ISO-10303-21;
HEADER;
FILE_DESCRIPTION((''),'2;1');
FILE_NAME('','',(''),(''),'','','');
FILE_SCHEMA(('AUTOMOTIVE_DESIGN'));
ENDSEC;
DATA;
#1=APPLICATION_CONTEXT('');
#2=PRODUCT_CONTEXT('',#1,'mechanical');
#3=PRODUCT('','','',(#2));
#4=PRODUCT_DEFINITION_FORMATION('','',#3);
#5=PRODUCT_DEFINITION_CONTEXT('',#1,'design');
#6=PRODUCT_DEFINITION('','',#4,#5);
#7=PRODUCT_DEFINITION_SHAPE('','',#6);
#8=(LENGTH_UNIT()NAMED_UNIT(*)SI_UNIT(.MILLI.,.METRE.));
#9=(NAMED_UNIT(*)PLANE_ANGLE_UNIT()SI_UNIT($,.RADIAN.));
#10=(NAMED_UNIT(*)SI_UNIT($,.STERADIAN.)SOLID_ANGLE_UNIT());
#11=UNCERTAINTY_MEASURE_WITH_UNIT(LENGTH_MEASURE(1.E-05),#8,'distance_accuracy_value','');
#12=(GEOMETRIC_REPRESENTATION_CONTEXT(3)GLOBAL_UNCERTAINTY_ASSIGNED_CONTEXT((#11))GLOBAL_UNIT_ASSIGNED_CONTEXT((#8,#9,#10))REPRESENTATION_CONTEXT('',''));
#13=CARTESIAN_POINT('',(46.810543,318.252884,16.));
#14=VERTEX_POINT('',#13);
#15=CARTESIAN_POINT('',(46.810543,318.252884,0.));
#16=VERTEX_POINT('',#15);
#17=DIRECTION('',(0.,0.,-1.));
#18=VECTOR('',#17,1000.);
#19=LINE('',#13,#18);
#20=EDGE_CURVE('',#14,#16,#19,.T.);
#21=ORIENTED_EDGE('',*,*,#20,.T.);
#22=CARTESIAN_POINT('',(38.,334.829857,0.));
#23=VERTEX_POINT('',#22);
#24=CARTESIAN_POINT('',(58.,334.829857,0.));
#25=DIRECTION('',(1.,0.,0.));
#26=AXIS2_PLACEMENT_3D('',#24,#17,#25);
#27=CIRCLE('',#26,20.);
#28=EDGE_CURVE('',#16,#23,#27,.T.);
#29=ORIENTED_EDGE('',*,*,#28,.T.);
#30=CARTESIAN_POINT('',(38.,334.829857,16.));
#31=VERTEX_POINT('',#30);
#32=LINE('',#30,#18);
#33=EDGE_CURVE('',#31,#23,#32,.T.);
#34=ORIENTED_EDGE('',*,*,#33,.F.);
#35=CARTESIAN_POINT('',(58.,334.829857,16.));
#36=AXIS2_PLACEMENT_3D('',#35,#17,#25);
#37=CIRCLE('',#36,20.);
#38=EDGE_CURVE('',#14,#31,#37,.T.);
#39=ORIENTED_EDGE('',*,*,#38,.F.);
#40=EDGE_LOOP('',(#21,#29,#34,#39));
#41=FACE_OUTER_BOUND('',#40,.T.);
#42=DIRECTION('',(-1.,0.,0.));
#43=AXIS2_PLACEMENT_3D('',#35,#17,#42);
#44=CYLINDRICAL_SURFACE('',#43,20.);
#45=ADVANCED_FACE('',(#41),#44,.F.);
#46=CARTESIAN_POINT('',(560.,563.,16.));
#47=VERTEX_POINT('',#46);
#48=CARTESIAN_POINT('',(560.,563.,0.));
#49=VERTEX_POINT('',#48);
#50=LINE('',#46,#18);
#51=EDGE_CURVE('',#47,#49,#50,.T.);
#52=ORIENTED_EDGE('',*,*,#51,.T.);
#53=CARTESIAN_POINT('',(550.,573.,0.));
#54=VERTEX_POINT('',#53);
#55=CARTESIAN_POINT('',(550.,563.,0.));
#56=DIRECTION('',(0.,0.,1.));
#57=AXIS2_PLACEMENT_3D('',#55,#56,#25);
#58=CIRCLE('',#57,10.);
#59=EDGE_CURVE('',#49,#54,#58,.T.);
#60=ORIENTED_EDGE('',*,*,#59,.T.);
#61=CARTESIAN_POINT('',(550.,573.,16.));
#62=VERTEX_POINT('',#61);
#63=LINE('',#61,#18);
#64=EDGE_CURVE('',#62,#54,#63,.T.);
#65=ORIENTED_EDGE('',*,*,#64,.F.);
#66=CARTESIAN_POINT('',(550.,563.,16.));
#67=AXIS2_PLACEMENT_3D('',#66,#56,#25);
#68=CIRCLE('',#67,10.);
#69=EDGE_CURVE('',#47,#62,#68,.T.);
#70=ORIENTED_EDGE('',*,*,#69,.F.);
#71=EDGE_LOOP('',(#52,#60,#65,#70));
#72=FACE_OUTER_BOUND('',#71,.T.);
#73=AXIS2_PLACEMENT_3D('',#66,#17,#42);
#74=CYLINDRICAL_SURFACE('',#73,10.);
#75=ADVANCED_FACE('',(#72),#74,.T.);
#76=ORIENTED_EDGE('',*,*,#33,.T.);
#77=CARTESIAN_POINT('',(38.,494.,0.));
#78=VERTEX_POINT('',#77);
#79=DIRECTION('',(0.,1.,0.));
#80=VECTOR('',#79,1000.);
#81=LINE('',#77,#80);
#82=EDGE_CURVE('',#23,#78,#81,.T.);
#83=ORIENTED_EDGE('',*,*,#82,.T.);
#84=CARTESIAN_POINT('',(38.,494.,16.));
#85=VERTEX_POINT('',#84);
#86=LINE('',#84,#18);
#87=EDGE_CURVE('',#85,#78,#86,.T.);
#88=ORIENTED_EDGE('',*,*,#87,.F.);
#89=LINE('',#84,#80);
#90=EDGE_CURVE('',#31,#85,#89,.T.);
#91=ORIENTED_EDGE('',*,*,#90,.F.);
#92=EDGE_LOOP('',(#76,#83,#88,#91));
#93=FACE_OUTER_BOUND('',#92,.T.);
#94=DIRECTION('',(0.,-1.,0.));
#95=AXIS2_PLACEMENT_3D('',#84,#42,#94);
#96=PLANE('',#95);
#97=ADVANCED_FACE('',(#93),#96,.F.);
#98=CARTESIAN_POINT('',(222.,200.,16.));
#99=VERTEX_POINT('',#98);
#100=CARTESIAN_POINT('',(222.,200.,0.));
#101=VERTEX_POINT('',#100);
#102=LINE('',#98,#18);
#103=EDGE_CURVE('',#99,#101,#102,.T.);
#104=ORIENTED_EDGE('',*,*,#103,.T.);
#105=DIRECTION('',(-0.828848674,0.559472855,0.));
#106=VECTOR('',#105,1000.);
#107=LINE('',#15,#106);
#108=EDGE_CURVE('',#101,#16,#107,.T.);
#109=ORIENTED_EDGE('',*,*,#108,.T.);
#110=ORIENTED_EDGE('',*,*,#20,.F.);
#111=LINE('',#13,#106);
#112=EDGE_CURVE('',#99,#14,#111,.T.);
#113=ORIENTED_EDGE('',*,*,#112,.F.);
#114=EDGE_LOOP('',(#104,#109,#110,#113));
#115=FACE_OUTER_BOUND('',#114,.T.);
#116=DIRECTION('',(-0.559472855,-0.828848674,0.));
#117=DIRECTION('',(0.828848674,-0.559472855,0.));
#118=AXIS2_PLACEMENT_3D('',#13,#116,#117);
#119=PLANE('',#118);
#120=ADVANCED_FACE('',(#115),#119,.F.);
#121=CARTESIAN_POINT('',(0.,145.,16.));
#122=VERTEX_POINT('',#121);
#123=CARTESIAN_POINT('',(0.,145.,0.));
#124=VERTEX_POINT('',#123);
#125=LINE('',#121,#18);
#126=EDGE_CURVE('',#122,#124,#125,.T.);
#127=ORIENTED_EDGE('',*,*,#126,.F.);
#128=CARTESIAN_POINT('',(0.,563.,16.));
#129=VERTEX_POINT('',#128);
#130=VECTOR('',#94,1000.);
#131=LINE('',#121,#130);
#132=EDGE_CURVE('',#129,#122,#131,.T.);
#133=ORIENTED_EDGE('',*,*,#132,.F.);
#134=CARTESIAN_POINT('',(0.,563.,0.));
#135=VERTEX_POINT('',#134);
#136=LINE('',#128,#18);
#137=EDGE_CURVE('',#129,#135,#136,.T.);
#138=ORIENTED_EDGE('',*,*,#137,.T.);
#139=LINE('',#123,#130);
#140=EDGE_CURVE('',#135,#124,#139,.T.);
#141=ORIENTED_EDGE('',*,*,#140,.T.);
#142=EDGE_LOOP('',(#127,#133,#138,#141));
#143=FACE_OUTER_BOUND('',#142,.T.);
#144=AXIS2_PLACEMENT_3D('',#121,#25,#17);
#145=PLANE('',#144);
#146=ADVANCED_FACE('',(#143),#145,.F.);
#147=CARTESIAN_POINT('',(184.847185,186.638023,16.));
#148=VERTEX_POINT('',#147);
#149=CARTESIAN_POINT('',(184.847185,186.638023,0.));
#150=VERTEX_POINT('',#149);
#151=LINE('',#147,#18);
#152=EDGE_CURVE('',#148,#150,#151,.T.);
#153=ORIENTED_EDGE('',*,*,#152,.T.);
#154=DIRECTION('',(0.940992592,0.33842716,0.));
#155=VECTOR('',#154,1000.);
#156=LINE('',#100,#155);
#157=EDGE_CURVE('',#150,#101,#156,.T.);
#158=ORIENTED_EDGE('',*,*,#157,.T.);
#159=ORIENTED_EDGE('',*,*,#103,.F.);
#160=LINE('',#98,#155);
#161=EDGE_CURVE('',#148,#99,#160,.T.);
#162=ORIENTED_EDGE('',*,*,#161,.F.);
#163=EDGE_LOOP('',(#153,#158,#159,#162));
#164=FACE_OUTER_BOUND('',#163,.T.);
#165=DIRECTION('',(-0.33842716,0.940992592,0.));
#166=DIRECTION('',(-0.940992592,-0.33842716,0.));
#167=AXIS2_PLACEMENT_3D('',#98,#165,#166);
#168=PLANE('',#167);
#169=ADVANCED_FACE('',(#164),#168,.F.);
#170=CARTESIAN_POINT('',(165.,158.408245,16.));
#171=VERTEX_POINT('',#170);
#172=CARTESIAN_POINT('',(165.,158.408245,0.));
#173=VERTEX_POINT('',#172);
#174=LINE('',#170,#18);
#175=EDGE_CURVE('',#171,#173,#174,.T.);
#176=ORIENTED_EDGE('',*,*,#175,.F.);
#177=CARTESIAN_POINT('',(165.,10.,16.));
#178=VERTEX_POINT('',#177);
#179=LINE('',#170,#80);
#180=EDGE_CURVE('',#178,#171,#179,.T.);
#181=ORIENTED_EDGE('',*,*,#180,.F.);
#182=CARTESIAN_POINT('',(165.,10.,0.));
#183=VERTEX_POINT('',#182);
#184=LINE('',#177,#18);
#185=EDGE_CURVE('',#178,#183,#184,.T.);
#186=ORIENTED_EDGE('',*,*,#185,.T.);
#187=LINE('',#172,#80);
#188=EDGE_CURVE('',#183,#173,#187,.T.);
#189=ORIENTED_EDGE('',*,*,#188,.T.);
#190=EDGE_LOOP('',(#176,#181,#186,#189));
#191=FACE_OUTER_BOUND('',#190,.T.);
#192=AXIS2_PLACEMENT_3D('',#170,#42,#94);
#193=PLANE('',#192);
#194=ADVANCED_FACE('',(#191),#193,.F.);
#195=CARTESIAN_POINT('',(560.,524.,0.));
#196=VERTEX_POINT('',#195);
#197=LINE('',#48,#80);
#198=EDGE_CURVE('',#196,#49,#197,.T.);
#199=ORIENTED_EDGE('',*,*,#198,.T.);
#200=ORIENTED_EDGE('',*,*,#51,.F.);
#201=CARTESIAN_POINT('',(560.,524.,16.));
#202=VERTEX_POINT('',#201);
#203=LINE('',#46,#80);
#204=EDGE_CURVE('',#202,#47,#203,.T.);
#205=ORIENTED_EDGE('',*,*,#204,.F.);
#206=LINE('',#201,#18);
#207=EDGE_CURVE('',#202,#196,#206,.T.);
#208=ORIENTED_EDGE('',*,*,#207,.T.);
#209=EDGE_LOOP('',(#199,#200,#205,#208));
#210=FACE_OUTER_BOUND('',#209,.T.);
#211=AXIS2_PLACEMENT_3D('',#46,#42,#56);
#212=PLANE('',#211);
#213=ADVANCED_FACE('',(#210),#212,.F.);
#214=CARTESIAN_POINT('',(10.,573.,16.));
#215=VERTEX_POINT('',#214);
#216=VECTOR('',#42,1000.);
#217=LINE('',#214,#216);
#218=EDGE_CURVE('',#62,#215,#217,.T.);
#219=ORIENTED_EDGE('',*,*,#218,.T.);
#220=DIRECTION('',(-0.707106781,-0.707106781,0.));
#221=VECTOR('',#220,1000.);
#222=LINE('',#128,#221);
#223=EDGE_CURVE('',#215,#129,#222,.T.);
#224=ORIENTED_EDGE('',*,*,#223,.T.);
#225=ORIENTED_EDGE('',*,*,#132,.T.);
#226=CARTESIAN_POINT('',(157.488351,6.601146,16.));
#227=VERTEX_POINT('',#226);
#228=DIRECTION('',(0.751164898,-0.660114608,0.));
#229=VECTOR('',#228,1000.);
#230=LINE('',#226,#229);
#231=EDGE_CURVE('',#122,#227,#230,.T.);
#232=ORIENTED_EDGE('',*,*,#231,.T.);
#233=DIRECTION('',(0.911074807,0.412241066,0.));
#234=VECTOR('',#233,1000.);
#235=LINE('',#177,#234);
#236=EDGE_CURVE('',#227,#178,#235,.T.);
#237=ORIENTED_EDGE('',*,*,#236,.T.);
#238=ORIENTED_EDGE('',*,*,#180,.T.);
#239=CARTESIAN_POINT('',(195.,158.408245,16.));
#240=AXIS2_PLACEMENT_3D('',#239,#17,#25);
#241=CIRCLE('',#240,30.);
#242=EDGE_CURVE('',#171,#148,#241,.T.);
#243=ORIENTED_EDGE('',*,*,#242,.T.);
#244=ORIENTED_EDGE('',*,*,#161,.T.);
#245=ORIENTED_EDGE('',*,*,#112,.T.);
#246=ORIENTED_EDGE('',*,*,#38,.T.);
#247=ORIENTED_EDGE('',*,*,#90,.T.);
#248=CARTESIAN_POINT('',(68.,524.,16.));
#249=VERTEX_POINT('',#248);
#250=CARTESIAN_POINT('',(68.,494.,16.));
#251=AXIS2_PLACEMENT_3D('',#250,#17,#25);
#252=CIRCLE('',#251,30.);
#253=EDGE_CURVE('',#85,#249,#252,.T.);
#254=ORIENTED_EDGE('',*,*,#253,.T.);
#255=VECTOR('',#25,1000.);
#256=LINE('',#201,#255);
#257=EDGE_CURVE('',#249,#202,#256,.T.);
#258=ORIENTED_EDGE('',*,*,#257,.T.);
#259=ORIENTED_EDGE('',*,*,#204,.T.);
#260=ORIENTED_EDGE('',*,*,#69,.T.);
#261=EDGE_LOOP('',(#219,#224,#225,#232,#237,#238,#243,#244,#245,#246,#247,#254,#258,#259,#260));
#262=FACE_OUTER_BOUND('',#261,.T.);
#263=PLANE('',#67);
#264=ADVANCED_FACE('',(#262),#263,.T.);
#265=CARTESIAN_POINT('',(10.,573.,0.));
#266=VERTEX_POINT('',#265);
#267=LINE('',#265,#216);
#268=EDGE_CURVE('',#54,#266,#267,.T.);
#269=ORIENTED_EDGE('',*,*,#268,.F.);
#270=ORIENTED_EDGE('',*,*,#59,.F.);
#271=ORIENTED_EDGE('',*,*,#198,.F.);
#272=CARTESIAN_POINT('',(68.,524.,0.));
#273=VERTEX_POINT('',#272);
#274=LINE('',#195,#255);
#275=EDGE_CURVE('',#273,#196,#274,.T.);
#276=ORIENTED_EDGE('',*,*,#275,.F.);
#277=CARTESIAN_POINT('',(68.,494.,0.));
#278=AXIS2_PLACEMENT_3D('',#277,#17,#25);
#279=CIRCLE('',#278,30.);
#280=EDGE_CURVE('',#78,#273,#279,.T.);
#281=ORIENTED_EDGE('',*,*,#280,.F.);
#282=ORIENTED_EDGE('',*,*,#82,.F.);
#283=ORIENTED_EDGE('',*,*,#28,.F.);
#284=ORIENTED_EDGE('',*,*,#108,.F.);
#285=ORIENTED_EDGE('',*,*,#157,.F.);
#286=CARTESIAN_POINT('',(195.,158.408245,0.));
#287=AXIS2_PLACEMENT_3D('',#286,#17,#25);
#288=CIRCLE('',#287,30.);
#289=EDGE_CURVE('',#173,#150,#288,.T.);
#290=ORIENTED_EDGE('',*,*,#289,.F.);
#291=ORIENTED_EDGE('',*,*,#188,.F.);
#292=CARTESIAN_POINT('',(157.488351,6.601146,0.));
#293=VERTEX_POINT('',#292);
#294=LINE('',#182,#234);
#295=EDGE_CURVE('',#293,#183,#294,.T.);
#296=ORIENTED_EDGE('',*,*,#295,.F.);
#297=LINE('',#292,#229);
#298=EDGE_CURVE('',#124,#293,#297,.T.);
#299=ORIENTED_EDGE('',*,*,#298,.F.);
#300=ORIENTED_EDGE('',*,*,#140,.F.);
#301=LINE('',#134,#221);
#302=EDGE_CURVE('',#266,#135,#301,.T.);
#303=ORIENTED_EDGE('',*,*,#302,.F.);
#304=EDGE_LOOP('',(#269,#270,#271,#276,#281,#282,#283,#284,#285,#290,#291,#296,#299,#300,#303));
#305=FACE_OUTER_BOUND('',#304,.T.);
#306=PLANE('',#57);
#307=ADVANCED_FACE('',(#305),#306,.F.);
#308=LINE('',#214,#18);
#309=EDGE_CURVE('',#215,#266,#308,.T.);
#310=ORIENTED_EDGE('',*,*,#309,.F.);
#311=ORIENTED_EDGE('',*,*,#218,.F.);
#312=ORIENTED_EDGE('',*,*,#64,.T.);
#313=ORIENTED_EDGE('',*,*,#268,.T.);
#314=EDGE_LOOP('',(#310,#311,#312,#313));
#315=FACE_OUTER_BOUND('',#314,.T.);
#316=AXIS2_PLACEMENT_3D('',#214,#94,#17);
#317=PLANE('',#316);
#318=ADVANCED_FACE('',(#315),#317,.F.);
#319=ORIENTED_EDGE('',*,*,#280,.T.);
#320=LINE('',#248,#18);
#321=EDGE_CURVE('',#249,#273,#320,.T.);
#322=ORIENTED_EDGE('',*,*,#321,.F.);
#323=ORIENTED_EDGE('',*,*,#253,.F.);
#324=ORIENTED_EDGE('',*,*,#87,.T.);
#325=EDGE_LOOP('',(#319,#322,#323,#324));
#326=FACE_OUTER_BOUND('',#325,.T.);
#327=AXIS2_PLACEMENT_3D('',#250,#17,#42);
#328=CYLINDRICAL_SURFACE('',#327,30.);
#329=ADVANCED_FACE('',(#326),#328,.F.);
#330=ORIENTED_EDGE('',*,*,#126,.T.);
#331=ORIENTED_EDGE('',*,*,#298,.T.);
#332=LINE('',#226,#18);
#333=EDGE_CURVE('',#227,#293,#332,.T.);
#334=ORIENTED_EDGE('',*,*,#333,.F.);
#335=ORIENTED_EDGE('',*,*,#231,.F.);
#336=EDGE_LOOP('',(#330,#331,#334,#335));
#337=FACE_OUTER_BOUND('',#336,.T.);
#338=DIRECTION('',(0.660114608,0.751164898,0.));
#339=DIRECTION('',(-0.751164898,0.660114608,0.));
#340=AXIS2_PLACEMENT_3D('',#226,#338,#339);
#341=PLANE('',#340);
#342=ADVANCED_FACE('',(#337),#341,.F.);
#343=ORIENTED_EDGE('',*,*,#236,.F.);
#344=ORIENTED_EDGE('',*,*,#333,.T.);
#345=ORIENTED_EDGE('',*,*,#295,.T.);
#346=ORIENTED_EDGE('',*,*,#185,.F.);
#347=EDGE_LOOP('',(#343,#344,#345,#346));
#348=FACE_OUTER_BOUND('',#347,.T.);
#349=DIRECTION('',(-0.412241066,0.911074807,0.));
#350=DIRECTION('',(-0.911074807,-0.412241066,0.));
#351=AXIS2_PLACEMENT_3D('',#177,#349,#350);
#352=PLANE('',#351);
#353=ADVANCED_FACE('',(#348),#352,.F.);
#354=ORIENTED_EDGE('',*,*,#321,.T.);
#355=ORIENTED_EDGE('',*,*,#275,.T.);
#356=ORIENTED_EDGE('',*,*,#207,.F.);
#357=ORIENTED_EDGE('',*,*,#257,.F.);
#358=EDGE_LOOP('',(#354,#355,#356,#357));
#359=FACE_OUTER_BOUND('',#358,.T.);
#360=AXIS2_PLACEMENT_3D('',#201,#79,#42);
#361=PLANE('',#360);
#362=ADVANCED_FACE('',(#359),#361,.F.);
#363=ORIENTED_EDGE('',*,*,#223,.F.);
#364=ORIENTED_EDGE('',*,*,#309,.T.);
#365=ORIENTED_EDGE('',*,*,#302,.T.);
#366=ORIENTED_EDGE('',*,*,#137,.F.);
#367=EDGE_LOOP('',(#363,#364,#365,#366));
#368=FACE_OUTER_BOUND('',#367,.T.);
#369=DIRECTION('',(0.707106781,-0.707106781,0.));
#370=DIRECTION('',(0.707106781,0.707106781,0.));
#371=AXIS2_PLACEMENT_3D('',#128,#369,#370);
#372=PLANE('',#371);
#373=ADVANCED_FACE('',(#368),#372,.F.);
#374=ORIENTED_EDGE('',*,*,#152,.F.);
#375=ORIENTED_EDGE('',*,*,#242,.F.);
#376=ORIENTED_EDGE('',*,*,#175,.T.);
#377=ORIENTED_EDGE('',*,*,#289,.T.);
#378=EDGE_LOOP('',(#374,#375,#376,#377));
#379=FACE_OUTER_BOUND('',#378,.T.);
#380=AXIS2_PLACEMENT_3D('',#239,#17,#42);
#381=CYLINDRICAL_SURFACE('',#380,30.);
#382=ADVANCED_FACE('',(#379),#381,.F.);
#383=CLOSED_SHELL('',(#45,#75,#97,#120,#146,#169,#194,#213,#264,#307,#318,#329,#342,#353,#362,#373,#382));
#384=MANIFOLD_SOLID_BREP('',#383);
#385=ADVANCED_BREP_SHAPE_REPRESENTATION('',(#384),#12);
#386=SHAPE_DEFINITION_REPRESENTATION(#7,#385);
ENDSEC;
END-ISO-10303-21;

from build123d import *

# Parameters (mm, degrees)
BOSS_EXTRUDE1_DEPTH = 16


with BuildPart() as part:
    # Sketch1 → Boss-Extrude1 (new body)
    with BuildSketch(Plane.XY):
        with BuildLine():
            Line((0, 145), (0, 563))
            Line((0, 563), (10, 573))
            Line((10, 573), (550, 573))
            ThreePointArc((550, 573), (557.071067812, 570.071067812), (560, 563))
            Line((560, 563), (560, 524))
            Line((560, 524), (68, 524))
            ThreePointArc((68, 524), (46.786796564, 515.213203436), (38, 494))
            Line((38, 494), (38, 334.829857024))
            ThreePointArc((38, 334.829857024), (40.33946289, 325.443407802), (46.8105429, 318.252883543))
            Line((46.8105429, 318.252883543), (222, 200))
            Line((222, 200), (184.847185197, 186.638022746))
            ThreePointArc((184.847185197, 186.638022746), (170.458357389, 175.662455442), (165, 158.408245001))
            Line((165, 158.408245001), (165, 10))
            Line((165, 10), (157.488351016, 6.601146077))
            Line((157.488351016, 6.601146077), (0, 145))
        make_face()
    extrude(amount=BOSS_EXTRUDE1_DEPTH)


solid = part.part
